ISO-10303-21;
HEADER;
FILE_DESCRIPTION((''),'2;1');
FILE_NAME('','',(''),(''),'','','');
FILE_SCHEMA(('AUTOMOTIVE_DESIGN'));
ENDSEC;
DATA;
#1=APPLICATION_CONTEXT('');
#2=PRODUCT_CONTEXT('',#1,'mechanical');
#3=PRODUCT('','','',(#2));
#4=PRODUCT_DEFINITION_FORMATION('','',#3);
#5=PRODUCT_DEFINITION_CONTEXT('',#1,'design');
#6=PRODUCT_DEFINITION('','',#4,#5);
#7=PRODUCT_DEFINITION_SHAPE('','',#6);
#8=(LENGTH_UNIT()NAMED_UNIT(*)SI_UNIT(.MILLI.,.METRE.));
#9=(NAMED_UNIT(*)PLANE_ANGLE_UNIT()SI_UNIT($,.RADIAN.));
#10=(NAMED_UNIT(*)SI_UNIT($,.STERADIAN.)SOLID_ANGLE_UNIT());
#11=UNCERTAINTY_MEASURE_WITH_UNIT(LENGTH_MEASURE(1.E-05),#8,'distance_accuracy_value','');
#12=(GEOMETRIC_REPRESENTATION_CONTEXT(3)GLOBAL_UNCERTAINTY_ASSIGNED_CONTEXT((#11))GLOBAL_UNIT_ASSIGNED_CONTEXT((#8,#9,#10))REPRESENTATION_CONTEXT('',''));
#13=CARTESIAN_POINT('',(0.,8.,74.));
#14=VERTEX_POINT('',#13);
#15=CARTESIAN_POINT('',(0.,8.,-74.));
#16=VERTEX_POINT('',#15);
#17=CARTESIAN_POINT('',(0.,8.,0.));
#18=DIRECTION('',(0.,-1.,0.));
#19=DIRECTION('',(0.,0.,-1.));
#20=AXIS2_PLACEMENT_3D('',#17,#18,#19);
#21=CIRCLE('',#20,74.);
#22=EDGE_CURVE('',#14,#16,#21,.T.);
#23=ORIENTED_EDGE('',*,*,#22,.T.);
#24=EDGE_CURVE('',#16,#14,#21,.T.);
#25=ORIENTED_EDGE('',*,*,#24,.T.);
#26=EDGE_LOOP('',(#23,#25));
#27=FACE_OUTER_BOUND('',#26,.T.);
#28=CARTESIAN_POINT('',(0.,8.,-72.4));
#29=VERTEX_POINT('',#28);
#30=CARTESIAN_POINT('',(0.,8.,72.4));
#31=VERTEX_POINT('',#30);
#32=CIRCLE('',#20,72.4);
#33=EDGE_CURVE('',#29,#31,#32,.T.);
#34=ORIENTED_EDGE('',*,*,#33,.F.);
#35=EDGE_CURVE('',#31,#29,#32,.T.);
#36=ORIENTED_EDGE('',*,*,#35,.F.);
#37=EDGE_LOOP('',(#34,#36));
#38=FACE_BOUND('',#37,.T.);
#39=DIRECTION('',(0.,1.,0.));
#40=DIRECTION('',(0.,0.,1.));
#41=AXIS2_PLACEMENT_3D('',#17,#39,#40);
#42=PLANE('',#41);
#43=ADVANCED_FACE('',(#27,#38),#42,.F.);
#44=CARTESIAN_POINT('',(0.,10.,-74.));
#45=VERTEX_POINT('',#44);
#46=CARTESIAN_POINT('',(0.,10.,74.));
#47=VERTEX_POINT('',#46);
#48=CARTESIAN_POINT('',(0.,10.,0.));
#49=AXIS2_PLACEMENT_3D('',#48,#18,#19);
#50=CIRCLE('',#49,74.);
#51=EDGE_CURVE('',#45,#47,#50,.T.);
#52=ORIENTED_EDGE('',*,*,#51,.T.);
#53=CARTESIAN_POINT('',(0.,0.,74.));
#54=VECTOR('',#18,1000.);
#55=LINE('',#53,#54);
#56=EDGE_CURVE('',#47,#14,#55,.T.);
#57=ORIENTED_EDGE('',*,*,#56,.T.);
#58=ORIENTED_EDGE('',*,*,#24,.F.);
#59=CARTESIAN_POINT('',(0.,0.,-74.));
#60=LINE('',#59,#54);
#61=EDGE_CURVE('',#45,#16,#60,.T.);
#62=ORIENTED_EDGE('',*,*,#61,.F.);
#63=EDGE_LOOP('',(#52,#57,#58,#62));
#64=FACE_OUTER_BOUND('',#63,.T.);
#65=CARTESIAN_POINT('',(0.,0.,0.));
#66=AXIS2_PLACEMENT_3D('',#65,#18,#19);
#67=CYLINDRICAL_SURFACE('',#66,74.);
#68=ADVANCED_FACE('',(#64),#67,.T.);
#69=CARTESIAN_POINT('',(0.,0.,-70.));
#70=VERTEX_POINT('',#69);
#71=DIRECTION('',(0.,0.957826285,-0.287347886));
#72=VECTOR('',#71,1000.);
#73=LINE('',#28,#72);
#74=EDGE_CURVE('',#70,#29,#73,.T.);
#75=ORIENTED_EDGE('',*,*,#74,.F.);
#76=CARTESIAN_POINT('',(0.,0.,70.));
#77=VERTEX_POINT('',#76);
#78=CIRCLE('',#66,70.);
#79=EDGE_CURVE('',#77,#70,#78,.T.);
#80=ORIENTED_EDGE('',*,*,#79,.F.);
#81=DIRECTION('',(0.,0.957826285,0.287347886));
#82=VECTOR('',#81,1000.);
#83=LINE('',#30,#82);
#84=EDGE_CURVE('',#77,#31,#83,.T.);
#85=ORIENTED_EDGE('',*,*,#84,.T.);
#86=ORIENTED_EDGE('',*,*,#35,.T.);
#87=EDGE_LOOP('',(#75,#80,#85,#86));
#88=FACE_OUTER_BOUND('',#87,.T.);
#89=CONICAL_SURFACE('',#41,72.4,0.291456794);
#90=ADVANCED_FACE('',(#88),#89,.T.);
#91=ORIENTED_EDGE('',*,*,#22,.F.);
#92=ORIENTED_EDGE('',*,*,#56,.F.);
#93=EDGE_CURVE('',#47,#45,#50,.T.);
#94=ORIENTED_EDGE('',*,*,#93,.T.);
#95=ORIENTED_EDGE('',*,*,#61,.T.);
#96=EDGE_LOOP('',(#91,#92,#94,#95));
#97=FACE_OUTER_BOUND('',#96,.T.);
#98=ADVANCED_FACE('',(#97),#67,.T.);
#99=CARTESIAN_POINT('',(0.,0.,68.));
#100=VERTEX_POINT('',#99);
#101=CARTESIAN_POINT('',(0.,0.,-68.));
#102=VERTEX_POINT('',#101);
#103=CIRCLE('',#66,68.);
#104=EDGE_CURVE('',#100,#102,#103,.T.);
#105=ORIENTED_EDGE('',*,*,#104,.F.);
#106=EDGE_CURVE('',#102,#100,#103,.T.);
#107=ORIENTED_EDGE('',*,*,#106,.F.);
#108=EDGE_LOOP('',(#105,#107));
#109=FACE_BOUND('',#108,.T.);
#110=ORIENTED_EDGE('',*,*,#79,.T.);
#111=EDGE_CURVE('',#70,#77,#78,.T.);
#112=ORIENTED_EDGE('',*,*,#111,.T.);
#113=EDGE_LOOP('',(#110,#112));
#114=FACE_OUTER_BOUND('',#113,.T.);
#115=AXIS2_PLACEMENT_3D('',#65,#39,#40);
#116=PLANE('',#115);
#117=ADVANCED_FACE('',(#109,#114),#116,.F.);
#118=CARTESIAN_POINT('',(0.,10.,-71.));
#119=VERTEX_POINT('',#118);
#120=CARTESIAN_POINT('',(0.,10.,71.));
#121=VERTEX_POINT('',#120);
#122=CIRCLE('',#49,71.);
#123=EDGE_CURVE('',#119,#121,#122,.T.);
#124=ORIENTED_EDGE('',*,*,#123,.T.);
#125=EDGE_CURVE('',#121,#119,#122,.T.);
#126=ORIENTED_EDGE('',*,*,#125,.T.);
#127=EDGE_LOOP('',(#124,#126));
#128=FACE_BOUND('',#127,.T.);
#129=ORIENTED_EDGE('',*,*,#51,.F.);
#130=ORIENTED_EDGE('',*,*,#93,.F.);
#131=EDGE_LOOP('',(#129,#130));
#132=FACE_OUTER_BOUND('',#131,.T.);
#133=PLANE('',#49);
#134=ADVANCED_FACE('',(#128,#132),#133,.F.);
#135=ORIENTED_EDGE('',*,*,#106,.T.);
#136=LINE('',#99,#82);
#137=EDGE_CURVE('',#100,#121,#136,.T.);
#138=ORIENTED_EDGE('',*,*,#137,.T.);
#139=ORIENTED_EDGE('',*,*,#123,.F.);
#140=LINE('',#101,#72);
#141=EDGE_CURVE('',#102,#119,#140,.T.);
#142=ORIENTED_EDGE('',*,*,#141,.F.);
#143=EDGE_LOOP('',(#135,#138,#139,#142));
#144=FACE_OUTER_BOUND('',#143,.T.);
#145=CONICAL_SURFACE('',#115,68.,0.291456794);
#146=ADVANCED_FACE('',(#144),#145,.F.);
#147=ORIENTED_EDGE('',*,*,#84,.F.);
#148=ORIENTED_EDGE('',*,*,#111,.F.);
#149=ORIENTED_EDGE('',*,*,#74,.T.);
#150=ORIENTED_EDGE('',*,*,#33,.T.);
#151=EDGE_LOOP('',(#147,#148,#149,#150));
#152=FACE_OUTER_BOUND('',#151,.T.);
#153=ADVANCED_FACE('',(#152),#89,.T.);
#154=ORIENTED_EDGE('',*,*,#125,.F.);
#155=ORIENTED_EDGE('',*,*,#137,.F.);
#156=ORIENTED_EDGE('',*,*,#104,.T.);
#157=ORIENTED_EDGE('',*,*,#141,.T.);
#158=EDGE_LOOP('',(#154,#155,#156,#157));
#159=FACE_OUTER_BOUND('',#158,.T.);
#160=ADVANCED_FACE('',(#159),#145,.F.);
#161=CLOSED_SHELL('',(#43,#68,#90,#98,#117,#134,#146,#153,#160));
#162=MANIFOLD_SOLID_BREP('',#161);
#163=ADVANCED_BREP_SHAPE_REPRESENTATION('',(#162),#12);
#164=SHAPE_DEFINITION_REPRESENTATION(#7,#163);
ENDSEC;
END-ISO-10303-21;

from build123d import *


with BuildPart() as part:
    # Sketch 5 → Revolve 1 (revolve)
    with BuildSketch(Plane.XY, mode=Mode.PRIVATE) as revolve_1_sk:
        Polygon((-68, 0), (-71, 10), (-74, 10), (-74, 8), (-72.4, 8), (-70, 0), align=None)
    revolve(revolve_1_sk.sketch.rotate(Axis((0, 0, 0), (0, 1, 0)), 270), axis=Axis((0, 0, 0), (0, 1, 0)))


solid = part.part
